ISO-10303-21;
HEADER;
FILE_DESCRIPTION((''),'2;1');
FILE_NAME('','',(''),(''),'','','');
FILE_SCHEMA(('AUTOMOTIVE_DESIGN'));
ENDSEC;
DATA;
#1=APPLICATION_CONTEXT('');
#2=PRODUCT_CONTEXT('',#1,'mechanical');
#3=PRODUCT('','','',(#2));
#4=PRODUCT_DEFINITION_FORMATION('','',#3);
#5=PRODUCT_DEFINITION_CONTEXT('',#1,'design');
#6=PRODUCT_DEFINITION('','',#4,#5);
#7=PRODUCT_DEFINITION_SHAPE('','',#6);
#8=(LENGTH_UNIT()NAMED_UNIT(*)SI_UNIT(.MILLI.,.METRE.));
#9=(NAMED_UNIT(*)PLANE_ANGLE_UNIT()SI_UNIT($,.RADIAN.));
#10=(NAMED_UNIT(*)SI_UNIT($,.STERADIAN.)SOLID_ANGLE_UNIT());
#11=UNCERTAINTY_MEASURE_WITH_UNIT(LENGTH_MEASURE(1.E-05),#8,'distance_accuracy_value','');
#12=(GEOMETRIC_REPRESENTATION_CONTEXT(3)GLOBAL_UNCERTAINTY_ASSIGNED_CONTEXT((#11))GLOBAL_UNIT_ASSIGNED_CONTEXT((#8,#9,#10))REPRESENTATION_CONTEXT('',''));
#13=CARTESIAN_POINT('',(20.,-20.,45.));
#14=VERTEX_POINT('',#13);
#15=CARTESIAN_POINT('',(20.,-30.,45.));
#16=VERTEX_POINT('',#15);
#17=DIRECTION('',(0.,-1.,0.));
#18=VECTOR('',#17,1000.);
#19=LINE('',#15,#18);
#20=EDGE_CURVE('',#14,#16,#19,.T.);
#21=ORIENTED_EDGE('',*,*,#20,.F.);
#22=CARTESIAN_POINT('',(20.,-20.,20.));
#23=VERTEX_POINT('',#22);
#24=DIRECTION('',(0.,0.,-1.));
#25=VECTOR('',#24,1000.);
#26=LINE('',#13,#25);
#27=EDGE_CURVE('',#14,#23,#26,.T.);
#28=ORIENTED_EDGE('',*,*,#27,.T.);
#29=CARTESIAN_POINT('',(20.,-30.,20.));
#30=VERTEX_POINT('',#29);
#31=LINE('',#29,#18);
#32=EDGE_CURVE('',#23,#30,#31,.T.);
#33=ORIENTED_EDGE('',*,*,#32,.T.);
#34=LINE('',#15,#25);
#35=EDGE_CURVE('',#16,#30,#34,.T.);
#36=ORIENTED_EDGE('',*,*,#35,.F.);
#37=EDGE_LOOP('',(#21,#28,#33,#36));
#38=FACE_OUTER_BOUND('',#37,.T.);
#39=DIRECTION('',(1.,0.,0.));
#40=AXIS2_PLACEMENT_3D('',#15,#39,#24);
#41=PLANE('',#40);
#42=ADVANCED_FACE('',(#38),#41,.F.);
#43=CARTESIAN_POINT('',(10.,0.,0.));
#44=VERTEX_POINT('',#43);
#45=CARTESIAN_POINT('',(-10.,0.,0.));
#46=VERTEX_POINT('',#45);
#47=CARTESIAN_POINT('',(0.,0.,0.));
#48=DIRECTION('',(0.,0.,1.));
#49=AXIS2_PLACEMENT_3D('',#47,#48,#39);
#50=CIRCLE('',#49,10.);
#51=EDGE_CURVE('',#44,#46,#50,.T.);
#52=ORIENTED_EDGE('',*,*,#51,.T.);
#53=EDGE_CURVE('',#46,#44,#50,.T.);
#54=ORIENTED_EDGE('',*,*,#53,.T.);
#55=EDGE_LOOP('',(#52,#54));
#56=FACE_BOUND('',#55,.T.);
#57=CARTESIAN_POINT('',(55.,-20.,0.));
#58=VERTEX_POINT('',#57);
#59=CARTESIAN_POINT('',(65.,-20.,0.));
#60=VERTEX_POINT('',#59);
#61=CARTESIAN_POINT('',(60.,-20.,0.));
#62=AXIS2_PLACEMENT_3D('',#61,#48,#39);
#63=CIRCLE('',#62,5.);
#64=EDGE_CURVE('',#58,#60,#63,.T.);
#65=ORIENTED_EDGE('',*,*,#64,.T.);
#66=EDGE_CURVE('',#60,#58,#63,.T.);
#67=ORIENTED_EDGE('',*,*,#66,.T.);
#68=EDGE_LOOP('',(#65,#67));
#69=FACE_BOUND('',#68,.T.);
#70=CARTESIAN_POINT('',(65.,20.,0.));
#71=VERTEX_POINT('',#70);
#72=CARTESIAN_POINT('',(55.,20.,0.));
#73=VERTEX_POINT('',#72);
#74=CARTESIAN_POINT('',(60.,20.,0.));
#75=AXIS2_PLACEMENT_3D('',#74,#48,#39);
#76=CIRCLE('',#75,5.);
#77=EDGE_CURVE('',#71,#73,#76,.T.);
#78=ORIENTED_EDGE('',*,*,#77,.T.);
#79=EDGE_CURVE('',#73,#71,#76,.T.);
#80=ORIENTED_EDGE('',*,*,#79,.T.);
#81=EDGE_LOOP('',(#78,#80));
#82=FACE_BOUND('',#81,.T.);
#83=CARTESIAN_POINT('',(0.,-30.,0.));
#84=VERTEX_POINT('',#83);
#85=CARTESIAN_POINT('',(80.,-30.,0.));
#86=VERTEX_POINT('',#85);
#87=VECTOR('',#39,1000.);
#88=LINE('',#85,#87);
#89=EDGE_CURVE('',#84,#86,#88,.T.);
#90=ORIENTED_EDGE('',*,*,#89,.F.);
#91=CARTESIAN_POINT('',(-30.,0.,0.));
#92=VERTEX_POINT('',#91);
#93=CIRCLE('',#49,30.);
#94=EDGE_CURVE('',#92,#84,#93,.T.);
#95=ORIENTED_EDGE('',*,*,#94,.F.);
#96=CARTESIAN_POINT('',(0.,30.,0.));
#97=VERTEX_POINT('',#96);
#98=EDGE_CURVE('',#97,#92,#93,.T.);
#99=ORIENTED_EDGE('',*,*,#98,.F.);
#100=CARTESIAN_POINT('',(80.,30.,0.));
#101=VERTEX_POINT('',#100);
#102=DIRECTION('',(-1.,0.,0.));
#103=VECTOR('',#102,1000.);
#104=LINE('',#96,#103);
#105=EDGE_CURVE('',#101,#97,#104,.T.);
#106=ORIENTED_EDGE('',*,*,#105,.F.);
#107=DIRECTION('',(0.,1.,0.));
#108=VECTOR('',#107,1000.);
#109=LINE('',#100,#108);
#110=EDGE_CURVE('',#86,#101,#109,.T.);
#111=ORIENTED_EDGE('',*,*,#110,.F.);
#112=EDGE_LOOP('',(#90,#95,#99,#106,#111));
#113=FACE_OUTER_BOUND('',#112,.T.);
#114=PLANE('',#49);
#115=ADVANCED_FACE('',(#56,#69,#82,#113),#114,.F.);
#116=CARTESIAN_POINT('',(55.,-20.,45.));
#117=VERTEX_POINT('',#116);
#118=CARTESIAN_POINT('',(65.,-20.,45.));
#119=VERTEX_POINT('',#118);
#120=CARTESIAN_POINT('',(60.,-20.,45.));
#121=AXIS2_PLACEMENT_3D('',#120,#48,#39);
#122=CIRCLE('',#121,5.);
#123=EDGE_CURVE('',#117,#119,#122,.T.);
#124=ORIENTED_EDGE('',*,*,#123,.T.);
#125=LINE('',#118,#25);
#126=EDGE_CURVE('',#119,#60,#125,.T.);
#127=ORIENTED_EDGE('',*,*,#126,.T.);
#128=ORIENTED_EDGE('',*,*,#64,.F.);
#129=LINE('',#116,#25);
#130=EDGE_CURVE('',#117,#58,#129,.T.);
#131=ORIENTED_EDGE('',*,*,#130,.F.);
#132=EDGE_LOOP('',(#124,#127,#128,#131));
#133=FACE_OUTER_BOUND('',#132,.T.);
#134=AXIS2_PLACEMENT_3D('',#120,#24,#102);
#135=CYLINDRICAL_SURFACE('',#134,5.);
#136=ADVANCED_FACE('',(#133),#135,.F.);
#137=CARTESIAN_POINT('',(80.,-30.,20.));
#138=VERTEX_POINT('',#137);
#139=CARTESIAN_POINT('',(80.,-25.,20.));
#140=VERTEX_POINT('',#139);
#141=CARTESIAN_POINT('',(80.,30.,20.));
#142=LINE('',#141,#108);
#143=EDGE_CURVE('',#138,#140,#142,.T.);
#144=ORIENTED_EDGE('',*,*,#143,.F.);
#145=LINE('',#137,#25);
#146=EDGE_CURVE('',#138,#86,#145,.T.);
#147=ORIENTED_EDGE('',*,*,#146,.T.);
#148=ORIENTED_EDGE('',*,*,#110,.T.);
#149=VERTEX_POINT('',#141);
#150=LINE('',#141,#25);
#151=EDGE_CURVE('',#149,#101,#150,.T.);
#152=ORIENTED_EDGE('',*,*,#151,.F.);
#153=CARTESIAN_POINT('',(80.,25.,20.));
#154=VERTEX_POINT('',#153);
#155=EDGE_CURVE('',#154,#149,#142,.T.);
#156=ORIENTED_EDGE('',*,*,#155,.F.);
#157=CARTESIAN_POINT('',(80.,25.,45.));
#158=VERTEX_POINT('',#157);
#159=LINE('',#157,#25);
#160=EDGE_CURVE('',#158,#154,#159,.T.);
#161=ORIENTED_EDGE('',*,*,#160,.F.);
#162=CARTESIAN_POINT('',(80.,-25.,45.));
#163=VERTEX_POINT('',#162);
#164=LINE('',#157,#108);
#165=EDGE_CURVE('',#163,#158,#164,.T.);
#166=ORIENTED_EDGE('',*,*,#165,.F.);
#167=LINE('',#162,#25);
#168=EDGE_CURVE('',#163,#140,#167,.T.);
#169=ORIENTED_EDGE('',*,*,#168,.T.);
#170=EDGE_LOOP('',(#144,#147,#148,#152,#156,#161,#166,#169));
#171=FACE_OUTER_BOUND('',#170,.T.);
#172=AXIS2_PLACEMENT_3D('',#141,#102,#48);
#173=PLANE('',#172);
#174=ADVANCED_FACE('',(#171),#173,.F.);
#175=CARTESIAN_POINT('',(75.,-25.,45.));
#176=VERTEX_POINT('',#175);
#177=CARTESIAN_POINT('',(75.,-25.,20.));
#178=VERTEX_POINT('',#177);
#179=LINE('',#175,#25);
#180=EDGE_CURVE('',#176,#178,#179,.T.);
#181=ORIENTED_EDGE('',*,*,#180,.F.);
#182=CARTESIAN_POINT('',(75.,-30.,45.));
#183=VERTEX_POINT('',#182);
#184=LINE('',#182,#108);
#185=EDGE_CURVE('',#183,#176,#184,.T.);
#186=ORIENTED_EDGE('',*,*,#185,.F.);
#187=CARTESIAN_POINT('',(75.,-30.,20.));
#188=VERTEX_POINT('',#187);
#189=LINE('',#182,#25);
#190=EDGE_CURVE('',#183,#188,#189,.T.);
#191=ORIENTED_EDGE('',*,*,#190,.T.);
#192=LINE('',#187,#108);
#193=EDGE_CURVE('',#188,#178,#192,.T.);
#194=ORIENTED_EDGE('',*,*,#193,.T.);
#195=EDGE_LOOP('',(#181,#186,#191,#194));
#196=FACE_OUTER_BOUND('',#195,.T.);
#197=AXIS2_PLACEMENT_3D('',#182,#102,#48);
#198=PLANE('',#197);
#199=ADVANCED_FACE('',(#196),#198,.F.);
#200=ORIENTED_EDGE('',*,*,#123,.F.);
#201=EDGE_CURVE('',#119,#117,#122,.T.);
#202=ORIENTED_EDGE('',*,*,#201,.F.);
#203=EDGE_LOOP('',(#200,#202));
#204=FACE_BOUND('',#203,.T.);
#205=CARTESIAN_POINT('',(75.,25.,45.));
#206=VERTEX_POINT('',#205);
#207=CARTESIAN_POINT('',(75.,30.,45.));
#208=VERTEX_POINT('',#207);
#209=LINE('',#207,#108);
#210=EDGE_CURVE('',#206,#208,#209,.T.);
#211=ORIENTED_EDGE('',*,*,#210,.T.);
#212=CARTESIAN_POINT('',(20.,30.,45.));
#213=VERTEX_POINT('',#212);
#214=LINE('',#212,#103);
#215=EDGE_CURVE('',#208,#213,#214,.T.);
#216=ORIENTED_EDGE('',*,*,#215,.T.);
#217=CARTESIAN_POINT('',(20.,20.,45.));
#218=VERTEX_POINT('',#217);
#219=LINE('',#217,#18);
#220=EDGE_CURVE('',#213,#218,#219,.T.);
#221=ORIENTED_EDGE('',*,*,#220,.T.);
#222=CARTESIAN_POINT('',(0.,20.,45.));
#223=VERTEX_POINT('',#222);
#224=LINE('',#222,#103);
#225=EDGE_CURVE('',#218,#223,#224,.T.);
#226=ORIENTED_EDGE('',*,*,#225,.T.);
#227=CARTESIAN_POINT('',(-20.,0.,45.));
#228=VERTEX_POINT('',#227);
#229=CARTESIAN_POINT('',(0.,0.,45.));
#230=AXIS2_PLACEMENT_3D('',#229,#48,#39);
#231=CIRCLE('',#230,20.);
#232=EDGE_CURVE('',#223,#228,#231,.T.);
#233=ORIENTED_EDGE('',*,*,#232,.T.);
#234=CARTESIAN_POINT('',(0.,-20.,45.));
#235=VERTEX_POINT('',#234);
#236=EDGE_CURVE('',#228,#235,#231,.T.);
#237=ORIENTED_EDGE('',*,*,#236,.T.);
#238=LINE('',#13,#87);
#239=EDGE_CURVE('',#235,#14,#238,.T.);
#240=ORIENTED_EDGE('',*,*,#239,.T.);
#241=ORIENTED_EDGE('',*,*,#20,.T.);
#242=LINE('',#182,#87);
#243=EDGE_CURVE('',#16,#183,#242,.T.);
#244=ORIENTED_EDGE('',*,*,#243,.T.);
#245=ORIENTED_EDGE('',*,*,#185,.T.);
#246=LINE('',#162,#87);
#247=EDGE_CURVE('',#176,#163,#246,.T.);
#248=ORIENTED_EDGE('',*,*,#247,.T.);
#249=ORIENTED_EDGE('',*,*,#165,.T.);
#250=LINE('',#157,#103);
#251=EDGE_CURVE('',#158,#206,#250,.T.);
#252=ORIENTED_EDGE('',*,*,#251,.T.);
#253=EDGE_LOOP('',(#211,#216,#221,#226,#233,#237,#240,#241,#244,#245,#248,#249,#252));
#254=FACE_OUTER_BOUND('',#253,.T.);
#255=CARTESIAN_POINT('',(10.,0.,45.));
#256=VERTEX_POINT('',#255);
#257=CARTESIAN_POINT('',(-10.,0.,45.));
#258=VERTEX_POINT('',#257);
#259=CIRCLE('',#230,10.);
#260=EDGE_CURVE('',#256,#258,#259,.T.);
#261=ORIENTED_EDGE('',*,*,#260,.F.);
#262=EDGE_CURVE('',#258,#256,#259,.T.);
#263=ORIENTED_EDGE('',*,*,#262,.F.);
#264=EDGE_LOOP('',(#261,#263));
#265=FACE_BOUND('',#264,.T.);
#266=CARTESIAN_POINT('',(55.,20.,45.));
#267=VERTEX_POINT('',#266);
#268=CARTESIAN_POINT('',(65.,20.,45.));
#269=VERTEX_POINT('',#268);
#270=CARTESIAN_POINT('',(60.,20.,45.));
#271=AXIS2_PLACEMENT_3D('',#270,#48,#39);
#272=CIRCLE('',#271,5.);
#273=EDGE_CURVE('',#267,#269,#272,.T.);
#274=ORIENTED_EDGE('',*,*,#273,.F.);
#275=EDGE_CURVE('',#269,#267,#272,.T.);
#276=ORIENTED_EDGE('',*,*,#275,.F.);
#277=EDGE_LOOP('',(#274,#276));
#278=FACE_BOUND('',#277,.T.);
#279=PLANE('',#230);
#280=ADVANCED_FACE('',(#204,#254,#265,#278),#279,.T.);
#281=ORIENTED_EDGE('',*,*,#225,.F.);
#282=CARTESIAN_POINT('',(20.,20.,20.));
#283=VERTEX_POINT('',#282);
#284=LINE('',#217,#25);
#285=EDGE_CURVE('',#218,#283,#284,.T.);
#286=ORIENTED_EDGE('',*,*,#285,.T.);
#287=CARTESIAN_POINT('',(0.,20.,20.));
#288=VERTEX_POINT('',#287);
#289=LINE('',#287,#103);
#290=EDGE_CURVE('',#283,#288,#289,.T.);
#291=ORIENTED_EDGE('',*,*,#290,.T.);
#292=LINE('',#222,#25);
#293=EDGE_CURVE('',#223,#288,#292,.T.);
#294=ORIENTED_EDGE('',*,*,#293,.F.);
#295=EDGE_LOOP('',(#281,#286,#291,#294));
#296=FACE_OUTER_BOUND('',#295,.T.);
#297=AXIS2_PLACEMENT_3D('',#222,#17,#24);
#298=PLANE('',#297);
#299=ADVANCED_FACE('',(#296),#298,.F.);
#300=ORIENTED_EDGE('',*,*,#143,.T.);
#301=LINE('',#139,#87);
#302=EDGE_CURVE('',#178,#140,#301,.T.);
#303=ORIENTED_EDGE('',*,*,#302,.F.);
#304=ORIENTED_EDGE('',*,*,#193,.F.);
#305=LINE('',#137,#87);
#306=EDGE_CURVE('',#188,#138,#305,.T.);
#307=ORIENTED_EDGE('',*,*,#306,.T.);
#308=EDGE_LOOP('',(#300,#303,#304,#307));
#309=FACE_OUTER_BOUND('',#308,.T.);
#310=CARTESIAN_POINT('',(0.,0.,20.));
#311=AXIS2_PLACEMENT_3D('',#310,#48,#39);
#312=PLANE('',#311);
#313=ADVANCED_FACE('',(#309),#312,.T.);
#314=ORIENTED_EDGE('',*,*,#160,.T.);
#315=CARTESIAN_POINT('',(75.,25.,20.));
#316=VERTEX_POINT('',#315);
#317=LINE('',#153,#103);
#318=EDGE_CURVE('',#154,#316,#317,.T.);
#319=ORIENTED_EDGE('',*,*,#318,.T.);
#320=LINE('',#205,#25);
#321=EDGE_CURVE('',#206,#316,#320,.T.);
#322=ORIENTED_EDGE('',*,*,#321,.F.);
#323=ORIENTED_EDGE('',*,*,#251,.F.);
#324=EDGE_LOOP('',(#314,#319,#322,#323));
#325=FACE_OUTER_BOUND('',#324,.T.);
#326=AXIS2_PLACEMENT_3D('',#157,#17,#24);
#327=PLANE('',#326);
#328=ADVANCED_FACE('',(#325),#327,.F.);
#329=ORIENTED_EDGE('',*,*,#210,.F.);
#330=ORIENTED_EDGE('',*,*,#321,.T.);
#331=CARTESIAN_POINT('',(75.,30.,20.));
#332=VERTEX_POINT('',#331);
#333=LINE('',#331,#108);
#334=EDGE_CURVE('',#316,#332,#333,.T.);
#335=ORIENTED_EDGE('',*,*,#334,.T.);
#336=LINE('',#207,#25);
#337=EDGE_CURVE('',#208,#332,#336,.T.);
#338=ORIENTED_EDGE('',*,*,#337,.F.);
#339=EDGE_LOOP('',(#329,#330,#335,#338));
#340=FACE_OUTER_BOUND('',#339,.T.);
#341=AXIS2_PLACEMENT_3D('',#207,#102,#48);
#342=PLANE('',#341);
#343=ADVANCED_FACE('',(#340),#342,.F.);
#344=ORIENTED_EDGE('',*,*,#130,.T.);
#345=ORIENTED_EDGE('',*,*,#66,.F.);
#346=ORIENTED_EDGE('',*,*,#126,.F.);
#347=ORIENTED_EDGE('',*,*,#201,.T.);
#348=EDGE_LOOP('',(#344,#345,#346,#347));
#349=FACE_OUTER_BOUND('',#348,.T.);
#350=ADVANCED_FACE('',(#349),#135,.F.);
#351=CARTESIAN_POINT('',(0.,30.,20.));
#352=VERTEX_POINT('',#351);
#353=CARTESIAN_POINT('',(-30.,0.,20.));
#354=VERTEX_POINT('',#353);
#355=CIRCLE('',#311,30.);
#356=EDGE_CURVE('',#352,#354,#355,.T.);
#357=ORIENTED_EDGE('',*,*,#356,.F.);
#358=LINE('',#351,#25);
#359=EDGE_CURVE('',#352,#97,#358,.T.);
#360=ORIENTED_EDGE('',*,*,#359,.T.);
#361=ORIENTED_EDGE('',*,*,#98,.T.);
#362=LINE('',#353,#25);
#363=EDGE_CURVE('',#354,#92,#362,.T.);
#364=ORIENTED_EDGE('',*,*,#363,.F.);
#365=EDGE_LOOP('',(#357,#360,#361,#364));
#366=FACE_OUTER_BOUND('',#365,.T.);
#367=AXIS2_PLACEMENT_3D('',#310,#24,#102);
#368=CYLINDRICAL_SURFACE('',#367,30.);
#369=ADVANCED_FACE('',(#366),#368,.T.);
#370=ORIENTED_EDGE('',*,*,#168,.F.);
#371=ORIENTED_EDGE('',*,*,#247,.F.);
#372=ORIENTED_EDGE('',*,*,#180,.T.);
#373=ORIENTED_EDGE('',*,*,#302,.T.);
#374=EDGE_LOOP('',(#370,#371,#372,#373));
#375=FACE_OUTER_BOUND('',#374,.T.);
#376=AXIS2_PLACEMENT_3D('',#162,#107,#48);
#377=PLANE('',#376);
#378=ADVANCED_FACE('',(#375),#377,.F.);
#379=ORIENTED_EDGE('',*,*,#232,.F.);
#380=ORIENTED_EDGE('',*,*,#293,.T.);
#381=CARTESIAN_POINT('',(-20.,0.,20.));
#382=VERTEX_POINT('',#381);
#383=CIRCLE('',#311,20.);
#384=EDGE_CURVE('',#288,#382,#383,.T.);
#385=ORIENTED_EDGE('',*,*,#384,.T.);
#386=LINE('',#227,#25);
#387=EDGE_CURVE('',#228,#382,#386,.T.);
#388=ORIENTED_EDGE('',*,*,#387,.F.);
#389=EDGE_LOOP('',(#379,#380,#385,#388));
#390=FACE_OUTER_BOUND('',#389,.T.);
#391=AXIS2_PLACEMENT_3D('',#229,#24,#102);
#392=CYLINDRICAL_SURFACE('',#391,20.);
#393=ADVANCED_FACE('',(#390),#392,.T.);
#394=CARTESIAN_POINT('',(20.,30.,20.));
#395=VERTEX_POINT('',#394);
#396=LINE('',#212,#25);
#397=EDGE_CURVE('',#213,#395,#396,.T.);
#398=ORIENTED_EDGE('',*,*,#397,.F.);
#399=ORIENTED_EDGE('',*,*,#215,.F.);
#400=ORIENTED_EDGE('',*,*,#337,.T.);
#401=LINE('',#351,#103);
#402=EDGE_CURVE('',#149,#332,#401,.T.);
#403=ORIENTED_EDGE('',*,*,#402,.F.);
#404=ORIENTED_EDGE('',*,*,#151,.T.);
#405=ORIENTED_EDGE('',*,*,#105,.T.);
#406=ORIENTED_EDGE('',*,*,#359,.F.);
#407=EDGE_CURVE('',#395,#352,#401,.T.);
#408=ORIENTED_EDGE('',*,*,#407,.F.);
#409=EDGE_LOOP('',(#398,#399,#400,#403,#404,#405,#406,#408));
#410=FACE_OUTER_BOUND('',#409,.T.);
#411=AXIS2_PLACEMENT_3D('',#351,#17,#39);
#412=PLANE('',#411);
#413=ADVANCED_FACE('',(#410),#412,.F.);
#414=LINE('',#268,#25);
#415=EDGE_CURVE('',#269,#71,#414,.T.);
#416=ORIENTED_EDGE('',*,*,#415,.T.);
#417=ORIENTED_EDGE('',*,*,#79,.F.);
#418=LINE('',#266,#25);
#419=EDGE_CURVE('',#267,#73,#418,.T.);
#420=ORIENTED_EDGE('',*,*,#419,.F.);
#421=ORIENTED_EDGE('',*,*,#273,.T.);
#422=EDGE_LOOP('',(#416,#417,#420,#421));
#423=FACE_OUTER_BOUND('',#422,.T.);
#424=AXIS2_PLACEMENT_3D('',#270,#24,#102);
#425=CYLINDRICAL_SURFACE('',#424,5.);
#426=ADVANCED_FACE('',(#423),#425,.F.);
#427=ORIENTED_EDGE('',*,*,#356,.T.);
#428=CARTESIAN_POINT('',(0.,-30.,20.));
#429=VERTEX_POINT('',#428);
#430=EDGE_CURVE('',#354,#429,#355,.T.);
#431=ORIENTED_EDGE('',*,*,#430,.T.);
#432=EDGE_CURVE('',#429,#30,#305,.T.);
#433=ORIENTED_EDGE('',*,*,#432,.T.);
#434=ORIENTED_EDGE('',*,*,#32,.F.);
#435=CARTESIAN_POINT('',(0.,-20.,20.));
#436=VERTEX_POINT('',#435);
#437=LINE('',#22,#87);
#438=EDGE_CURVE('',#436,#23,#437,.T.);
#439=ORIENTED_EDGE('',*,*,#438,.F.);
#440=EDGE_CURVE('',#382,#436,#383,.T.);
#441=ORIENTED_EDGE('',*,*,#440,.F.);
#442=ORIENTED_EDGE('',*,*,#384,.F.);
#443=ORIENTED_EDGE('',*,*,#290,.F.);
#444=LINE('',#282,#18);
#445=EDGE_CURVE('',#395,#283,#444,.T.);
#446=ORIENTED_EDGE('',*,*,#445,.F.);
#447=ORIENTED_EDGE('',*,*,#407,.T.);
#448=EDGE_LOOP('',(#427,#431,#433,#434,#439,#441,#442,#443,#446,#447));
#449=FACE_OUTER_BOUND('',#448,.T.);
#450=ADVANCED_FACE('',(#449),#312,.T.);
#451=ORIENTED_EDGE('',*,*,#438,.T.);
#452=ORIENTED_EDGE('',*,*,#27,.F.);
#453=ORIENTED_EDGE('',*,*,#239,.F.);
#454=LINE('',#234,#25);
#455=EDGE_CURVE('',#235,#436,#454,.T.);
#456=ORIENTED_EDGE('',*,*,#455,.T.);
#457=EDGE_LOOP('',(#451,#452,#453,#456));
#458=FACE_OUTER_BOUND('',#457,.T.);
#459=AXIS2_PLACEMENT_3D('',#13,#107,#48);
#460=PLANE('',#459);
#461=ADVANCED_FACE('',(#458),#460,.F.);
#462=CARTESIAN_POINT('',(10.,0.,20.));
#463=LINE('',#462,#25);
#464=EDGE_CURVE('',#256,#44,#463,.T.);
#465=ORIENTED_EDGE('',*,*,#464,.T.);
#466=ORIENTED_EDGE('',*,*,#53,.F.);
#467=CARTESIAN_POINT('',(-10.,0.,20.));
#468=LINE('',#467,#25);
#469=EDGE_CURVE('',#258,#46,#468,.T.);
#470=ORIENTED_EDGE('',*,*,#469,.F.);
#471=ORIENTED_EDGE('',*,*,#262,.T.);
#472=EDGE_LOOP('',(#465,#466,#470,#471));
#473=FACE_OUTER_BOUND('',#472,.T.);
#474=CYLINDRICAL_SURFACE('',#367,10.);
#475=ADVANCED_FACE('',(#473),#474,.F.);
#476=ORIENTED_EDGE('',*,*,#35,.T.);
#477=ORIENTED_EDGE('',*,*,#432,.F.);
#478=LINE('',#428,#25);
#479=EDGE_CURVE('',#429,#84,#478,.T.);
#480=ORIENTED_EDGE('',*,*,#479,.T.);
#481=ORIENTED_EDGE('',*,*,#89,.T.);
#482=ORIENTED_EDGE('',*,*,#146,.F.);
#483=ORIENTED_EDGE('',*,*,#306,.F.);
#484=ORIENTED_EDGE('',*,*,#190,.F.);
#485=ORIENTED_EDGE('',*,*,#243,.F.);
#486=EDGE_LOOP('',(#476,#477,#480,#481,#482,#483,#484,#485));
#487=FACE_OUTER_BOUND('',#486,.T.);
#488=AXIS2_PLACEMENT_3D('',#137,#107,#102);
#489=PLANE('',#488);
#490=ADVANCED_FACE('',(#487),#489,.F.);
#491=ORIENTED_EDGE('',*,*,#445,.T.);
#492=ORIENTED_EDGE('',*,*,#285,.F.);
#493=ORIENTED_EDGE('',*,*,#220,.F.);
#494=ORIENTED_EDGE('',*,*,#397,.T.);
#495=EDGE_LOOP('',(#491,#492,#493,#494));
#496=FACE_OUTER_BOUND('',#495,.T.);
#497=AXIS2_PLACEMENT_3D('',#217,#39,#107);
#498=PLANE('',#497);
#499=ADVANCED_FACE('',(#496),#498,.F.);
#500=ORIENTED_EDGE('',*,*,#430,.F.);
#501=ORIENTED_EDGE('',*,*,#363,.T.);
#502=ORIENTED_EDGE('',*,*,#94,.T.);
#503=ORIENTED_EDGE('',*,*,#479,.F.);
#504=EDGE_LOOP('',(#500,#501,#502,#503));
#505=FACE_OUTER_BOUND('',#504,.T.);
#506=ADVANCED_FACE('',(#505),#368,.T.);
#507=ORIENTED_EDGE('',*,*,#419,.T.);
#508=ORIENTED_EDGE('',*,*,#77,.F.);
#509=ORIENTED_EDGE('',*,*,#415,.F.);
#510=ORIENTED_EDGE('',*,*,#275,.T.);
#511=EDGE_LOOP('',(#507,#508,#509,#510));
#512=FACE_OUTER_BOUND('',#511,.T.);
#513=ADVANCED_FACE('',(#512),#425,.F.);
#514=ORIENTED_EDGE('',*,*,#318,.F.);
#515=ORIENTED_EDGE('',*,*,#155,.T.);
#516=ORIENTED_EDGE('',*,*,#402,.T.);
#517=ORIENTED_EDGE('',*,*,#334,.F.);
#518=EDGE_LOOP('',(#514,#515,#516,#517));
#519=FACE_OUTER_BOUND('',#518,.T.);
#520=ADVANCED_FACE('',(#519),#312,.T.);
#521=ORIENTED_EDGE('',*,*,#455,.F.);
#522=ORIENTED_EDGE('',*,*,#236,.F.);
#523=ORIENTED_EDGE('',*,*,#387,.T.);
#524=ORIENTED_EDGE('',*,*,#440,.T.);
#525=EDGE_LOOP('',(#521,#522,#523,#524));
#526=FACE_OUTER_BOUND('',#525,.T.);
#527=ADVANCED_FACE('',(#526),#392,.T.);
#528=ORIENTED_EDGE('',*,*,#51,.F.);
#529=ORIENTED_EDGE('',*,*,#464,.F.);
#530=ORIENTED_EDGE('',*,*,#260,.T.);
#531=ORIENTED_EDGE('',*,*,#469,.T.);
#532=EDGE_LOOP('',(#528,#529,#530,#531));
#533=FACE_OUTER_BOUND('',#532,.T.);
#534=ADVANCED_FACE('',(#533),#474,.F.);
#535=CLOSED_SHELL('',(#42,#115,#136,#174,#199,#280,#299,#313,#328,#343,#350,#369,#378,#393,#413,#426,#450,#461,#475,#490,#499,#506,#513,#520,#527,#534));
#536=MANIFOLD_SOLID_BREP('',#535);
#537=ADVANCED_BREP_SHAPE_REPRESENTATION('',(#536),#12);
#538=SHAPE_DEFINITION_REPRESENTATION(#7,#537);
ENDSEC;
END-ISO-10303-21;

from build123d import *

# Parameters (mm, degrees)
BASE_BLOCK_SKETCH_R       = 10
BASE_BLOCK_DEPTH          = 20
LUG_BOSS_SKETCH_R         = 10
LUG_BOSS_SKETCH_R_2       = 5
LUG_BOSS_WITH_HOLES_DEPTH = 25
SLOT_CUT_SKETCH_R         = 5
SLOT_CUT_DEPTH            = 97.566039579


with BuildPart() as part:
    # Base Block Sketch → Base Block (new body)
    with BuildSketch(Plane.XY):
        with BuildLine():
            Line((0, 30), (80, 30))
            Line((80, 30), (80, -30))
            Line((80, -30), (0, -30))
            ThreePointArc((0, -30), (-30, 0), (0, 30))
        make_face()
        Circle(BASE_BLOCK_SKETCH_R, mode=Mode.SUBTRACT)
    extrude(amount=BASE_BLOCK_DEPTH)

    # Lug Boss Sketch → Lug Boss With Holes (add)
    with BuildSketch(Plane.XY.offset(20)):
        with BuildLine():
            Line((0, 20), (20, 20))
            Line((20, 20), (20, 30))
            Line((20, 30), (75, 30))
            Line((75, 30), (75, 25))
            Line((75, 25), (80, 25))
            Line((80, 25), (80, -25))
            Line((80, -25), (75, -25))
            Line((75, -25), (75, -30))
            Line((75, -30), (20, -30))
            Line((20, -30), (20, -20))
            Line((20, -20), (0, -20))
            ThreePointArc((0, -20), (-20, 0), (0, 20))
        make_face()
        Circle(LUG_BOSS_SKETCH_R, mode=Mode.SUBTRACT)
        with Locations((60, 20)):
            Circle(LUG_BOSS_SKETCH_R_2, mode=Mode.SUBTRACT)
        with Locations((60, -20)):
            Circle(LUG_BOSS_SKETCH_R_2, mode=Mode.SUBTRACT)
    extrude(amount=LUG_BOSS_WITH_HOLES_DEPTH)

    # Slot Cut Sketch → Slot Cut (cut, through all)
    with BuildSketch(Plane.XY.offset(45)):
        with Locations((60, -20)):
            Circle(SLOT_CUT_SKETCH_R)
        with Locations((60, 20)):
            Circle(SLOT_CUT_SKETCH_R)
    extrude(amount=-SLOT_CUT_DEPTH, mode=Mode.SUBTRACT)


solid = part.part
